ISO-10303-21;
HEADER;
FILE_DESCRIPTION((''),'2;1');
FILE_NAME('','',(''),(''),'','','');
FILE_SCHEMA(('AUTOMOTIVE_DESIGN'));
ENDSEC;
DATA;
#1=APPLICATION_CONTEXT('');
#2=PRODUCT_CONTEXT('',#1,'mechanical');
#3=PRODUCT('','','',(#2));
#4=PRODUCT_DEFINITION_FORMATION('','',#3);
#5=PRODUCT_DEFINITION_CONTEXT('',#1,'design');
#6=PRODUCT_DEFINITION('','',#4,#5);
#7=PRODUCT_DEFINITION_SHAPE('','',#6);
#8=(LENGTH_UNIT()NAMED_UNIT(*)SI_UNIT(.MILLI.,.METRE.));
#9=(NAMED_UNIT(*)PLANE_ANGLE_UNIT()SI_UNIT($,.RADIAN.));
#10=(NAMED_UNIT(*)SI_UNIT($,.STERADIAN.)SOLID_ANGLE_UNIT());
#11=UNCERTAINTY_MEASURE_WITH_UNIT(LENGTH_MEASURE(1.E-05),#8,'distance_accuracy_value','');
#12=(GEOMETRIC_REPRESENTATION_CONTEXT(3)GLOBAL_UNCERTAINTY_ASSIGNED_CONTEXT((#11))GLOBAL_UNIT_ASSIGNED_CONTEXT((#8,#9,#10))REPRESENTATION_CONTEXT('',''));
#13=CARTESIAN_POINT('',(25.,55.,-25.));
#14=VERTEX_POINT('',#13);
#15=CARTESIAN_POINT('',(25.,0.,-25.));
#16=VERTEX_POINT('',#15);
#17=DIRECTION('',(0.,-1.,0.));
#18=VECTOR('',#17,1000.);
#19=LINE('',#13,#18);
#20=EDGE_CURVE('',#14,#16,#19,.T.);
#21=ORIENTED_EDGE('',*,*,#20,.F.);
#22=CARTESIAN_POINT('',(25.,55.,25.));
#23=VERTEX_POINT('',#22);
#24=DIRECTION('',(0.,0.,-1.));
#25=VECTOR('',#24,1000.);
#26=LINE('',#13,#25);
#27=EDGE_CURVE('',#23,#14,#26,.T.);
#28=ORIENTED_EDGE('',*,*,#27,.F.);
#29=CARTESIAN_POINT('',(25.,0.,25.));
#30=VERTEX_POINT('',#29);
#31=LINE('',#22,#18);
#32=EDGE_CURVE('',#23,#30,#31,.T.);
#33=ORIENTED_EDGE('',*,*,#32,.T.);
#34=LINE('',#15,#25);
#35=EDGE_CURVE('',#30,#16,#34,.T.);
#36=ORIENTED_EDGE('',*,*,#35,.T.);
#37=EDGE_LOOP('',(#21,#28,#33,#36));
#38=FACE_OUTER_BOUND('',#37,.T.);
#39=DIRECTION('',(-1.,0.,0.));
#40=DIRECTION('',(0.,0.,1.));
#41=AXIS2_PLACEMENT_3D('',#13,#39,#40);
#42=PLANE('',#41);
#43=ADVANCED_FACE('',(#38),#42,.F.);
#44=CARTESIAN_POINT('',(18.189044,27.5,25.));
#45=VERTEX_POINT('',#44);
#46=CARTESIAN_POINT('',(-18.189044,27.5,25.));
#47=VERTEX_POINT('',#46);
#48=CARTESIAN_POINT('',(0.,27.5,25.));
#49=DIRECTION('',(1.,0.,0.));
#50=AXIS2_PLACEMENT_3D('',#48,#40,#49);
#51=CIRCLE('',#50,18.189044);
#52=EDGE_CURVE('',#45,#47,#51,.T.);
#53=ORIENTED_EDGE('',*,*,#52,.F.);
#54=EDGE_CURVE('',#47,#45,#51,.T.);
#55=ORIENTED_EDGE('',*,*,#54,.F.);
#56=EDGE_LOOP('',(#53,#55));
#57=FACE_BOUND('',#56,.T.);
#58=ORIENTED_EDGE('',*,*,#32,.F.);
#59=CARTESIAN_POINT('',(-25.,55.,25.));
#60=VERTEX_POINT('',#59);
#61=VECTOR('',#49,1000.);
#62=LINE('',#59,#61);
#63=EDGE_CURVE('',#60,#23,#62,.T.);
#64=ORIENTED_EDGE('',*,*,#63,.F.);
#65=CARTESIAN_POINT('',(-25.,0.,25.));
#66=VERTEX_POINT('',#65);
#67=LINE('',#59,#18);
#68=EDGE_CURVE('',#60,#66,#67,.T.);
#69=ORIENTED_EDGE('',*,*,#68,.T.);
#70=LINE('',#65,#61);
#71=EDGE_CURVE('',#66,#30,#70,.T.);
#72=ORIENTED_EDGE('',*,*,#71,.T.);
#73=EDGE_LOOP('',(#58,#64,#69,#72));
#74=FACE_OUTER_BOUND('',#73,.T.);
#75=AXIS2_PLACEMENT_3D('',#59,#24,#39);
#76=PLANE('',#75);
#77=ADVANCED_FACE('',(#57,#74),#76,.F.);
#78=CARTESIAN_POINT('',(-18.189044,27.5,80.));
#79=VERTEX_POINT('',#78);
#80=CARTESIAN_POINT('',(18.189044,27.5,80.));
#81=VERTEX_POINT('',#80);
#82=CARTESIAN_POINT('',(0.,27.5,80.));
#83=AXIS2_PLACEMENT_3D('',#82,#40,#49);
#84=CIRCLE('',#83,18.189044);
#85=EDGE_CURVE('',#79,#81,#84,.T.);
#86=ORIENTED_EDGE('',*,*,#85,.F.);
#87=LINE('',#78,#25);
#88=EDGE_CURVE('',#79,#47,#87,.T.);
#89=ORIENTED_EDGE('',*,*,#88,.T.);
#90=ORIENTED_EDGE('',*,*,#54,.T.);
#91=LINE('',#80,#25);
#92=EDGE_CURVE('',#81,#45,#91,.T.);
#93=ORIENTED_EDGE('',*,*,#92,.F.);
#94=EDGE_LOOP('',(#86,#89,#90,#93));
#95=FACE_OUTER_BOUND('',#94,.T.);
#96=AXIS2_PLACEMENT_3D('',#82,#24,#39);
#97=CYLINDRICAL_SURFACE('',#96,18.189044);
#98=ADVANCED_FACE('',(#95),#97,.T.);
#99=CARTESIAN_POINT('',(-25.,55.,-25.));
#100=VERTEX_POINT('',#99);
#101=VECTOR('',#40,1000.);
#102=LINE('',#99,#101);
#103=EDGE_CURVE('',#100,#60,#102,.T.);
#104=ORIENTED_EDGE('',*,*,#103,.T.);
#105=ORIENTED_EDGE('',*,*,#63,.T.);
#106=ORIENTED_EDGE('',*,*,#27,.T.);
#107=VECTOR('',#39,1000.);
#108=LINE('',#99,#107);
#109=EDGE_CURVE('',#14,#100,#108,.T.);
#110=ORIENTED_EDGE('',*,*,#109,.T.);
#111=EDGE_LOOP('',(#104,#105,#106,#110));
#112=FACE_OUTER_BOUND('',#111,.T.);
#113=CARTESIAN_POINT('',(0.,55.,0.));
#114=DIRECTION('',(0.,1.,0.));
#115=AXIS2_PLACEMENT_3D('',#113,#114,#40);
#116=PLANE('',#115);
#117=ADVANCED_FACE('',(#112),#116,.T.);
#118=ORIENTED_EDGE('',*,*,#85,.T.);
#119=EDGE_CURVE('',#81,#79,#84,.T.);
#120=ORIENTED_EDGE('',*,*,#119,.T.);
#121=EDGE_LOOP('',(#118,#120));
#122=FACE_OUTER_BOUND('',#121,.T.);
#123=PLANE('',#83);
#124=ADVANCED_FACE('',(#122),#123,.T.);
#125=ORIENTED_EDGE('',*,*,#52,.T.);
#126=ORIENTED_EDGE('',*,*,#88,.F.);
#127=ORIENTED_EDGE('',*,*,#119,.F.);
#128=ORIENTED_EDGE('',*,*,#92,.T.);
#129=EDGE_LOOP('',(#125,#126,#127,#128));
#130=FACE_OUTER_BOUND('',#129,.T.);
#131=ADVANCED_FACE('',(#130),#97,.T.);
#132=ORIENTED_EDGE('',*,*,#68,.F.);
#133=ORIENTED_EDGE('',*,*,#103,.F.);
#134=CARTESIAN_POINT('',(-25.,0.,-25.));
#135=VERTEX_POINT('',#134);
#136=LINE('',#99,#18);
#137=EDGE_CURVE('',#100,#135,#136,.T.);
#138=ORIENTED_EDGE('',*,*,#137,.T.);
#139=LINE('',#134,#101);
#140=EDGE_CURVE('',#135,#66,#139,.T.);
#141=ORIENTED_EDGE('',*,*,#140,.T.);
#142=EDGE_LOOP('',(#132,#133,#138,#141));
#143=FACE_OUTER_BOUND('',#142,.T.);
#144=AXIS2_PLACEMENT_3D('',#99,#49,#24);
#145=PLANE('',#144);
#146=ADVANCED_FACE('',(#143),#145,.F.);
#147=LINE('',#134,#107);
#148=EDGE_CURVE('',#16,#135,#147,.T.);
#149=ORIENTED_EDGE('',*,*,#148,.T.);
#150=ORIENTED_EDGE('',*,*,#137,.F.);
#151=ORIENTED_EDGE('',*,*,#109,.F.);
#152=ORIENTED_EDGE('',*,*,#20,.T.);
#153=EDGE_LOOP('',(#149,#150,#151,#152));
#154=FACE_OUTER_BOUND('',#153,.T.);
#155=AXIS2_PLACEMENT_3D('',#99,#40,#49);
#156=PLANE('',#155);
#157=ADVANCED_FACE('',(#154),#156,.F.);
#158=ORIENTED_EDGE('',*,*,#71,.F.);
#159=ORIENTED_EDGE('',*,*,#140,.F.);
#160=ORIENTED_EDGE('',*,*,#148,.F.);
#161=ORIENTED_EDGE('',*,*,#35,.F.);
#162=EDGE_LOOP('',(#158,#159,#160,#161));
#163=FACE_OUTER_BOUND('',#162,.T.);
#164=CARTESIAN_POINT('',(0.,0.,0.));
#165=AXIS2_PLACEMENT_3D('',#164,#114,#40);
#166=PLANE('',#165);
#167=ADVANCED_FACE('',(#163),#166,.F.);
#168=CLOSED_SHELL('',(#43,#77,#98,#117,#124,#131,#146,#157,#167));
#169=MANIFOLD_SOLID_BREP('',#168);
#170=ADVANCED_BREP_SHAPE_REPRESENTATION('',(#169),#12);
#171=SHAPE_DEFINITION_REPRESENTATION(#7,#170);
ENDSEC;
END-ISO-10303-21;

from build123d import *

# Parameters (mm, degrees)
SKETCH1_W           = 50
SKETCH1_H           = 50
BOSS_EXTRUDE1_DEPTH = 55
SKETCH2_R           = 18.189043711
BOSS_EXTRUDE2_DEPTH = 55


with BuildPart() as part:
    # Sketch1 → Boss-Extrude1 (new body)
    with BuildSketch(Plane(origin=(0, 0, 0), x_dir=(1, 0, 0), z_dir=(0, 1, 0))):
        Rectangle(SKETCH1_W, SKETCH1_H)
    extrude(amount=BOSS_EXTRUDE1_DEPTH)

    # Sketch2 → Boss-Extrude2 (add)
    with BuildSketch(Plane.XY.offset(25)):
        with Locations((0, 27.5)):
            Circle(SKETCH2_R)
    extrude(amount=BOSS_EXTRUDE2_DEPTH)


solid = part.part
